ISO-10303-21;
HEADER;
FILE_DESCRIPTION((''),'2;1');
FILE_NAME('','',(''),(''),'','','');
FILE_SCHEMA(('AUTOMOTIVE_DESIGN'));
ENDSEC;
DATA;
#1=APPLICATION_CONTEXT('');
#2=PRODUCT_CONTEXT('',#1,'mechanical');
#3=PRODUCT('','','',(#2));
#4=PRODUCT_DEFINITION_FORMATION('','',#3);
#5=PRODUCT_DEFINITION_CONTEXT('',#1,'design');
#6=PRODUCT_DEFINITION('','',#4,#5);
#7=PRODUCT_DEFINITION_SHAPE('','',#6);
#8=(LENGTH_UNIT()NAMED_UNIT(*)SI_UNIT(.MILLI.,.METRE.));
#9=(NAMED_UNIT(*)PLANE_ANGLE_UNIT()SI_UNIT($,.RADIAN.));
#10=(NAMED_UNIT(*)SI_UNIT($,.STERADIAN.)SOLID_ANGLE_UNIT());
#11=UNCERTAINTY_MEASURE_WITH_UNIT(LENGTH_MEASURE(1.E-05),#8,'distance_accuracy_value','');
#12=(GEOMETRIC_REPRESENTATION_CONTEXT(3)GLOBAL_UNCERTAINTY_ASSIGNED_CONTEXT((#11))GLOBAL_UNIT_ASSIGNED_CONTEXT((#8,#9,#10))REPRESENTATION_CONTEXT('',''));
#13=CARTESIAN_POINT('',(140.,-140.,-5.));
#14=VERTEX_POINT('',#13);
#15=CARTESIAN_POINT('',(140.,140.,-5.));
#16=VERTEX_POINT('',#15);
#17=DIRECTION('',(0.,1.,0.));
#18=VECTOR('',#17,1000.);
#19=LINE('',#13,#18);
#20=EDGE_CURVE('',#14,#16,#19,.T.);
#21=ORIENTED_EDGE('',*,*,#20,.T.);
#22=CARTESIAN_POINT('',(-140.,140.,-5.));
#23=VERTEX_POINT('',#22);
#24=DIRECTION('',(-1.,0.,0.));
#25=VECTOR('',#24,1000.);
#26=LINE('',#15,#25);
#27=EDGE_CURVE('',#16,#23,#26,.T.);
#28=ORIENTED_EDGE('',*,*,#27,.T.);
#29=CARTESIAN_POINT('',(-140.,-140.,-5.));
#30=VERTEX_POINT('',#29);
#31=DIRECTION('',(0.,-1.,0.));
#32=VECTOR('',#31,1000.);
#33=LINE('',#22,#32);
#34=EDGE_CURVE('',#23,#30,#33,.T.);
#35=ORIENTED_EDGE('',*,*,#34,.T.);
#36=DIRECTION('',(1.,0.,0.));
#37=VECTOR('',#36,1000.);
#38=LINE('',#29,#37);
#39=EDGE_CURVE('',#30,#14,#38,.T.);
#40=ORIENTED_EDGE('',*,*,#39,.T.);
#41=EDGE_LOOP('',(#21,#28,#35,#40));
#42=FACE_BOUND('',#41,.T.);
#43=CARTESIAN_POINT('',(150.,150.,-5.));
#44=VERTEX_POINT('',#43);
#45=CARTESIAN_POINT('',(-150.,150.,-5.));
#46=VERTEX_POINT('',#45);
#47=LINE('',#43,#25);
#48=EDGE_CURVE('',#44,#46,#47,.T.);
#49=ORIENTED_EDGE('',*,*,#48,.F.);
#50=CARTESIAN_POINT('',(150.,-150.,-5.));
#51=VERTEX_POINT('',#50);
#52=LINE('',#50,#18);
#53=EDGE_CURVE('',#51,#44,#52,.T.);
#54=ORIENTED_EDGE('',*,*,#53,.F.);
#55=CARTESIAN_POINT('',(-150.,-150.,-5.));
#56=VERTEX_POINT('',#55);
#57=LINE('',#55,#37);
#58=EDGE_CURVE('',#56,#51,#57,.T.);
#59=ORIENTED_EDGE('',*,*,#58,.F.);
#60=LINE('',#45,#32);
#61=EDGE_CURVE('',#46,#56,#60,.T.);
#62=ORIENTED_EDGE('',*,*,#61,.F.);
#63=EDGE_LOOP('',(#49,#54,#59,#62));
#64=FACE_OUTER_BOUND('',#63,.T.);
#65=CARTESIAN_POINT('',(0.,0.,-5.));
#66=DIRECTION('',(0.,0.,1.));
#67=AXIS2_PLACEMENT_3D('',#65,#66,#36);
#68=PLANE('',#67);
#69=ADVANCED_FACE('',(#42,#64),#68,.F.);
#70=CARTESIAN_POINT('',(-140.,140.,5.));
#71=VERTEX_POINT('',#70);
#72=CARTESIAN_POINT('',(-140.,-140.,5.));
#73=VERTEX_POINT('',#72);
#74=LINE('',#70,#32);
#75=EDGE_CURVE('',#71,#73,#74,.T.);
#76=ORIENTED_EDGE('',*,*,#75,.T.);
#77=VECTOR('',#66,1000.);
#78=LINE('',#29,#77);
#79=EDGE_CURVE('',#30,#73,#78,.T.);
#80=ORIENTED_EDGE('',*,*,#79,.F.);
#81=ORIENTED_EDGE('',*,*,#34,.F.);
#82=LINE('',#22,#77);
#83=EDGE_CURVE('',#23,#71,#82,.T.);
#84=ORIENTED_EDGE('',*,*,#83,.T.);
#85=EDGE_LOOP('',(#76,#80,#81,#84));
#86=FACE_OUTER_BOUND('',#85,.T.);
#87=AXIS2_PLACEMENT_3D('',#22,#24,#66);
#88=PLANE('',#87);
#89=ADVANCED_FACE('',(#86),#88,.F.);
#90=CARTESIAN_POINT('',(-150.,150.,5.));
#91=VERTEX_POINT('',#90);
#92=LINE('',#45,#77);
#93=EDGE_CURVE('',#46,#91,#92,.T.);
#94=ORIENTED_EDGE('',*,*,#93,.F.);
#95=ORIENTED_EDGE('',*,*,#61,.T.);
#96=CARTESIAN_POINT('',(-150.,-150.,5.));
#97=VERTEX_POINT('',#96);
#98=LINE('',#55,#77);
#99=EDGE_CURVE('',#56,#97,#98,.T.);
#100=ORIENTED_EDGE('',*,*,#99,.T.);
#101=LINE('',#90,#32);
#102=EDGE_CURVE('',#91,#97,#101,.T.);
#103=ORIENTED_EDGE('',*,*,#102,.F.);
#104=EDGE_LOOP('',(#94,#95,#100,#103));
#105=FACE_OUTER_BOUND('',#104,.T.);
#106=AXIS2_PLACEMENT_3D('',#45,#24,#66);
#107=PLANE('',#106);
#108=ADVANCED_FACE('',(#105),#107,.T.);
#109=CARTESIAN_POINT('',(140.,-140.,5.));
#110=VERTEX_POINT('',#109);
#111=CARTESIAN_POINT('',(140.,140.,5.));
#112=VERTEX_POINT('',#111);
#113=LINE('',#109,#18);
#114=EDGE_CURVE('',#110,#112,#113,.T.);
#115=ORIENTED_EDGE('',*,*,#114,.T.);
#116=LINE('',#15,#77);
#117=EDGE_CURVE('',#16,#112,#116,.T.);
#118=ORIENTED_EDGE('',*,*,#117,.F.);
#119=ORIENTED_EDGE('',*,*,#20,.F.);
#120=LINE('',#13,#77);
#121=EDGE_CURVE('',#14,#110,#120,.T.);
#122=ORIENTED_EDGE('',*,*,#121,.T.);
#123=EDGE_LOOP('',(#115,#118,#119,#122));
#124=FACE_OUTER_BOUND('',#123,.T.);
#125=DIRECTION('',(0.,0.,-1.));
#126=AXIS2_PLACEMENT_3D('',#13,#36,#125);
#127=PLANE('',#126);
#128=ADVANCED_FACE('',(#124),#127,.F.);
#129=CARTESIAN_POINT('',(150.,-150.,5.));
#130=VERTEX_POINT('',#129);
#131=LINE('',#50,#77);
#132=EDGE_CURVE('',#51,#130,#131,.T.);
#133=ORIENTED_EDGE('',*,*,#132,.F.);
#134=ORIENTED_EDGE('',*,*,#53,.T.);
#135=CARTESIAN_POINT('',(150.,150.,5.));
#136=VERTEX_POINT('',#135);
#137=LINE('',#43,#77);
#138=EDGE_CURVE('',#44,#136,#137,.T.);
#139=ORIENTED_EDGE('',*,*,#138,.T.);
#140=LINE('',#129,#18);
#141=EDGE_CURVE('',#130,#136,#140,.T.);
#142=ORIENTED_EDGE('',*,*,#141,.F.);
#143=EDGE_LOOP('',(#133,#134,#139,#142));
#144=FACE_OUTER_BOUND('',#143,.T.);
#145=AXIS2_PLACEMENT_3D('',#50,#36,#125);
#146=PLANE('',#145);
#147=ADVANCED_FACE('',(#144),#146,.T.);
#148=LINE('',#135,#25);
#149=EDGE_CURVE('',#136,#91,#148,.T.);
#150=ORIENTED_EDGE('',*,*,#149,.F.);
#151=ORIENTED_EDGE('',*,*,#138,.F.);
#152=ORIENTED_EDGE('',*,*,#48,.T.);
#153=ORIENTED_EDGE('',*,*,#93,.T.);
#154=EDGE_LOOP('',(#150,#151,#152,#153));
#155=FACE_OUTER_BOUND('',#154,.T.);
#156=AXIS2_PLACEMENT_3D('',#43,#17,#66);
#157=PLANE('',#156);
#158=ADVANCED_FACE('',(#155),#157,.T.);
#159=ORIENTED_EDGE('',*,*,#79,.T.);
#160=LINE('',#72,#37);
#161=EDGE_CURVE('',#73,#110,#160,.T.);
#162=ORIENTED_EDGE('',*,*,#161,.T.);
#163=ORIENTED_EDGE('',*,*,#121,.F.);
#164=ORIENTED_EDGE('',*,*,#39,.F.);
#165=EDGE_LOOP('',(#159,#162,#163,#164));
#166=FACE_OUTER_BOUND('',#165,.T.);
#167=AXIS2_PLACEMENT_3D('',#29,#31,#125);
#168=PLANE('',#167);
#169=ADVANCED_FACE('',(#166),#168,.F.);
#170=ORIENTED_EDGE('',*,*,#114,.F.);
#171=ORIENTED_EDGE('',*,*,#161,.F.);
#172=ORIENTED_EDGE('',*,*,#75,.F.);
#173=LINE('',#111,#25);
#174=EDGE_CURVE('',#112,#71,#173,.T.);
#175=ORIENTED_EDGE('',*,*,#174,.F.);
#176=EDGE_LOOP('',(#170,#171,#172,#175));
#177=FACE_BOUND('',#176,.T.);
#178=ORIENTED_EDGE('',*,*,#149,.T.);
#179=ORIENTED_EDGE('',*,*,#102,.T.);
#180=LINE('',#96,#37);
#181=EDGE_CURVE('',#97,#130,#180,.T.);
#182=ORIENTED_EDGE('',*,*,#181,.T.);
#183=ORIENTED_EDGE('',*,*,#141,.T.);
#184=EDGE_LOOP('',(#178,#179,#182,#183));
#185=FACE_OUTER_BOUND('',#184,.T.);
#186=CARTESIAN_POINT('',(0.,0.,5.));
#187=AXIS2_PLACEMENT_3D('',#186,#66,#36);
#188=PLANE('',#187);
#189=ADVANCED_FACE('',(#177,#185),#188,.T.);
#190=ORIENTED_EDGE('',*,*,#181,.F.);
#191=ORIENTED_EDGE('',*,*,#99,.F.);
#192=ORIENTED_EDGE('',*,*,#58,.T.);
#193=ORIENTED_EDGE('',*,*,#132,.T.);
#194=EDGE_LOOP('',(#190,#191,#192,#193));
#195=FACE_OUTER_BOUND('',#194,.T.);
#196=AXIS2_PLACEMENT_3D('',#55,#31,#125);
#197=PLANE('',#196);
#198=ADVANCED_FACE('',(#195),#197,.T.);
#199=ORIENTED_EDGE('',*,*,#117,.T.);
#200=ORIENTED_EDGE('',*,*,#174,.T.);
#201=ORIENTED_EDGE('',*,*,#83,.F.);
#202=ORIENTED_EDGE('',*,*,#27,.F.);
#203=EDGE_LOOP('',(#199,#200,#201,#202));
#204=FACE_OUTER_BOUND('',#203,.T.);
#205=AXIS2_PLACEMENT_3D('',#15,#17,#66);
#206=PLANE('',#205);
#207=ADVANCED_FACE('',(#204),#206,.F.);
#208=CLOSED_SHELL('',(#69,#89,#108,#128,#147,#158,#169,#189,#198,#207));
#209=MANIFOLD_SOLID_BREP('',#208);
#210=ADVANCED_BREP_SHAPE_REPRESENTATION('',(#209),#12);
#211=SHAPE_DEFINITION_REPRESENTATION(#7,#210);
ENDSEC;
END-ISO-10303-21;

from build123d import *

# Parameters (mm, degrees)
SKETCH_1_W      = 300
SKETCH_1_H      = 300
SKETCH_1_W_2    = 280
SKETCH_1_H_2    = 280
EXTRUDE_1_DEPTH = 5


with BuildPart() as part:
    # 草图1 → 凸台-拉伸1 (new, symmetric)
    with BuildSketch(Plane.XY):
        Rectangle(SKETCH_1_W, SKETCH_1_H)
        Rectangle(SKETCH_1_W_2, SKETCH_1_H_2, mode=Mode.SUBTRACT)
    extrude(amount=EXTRUDE_1_DEPTH, both=True)


solid = part.part
